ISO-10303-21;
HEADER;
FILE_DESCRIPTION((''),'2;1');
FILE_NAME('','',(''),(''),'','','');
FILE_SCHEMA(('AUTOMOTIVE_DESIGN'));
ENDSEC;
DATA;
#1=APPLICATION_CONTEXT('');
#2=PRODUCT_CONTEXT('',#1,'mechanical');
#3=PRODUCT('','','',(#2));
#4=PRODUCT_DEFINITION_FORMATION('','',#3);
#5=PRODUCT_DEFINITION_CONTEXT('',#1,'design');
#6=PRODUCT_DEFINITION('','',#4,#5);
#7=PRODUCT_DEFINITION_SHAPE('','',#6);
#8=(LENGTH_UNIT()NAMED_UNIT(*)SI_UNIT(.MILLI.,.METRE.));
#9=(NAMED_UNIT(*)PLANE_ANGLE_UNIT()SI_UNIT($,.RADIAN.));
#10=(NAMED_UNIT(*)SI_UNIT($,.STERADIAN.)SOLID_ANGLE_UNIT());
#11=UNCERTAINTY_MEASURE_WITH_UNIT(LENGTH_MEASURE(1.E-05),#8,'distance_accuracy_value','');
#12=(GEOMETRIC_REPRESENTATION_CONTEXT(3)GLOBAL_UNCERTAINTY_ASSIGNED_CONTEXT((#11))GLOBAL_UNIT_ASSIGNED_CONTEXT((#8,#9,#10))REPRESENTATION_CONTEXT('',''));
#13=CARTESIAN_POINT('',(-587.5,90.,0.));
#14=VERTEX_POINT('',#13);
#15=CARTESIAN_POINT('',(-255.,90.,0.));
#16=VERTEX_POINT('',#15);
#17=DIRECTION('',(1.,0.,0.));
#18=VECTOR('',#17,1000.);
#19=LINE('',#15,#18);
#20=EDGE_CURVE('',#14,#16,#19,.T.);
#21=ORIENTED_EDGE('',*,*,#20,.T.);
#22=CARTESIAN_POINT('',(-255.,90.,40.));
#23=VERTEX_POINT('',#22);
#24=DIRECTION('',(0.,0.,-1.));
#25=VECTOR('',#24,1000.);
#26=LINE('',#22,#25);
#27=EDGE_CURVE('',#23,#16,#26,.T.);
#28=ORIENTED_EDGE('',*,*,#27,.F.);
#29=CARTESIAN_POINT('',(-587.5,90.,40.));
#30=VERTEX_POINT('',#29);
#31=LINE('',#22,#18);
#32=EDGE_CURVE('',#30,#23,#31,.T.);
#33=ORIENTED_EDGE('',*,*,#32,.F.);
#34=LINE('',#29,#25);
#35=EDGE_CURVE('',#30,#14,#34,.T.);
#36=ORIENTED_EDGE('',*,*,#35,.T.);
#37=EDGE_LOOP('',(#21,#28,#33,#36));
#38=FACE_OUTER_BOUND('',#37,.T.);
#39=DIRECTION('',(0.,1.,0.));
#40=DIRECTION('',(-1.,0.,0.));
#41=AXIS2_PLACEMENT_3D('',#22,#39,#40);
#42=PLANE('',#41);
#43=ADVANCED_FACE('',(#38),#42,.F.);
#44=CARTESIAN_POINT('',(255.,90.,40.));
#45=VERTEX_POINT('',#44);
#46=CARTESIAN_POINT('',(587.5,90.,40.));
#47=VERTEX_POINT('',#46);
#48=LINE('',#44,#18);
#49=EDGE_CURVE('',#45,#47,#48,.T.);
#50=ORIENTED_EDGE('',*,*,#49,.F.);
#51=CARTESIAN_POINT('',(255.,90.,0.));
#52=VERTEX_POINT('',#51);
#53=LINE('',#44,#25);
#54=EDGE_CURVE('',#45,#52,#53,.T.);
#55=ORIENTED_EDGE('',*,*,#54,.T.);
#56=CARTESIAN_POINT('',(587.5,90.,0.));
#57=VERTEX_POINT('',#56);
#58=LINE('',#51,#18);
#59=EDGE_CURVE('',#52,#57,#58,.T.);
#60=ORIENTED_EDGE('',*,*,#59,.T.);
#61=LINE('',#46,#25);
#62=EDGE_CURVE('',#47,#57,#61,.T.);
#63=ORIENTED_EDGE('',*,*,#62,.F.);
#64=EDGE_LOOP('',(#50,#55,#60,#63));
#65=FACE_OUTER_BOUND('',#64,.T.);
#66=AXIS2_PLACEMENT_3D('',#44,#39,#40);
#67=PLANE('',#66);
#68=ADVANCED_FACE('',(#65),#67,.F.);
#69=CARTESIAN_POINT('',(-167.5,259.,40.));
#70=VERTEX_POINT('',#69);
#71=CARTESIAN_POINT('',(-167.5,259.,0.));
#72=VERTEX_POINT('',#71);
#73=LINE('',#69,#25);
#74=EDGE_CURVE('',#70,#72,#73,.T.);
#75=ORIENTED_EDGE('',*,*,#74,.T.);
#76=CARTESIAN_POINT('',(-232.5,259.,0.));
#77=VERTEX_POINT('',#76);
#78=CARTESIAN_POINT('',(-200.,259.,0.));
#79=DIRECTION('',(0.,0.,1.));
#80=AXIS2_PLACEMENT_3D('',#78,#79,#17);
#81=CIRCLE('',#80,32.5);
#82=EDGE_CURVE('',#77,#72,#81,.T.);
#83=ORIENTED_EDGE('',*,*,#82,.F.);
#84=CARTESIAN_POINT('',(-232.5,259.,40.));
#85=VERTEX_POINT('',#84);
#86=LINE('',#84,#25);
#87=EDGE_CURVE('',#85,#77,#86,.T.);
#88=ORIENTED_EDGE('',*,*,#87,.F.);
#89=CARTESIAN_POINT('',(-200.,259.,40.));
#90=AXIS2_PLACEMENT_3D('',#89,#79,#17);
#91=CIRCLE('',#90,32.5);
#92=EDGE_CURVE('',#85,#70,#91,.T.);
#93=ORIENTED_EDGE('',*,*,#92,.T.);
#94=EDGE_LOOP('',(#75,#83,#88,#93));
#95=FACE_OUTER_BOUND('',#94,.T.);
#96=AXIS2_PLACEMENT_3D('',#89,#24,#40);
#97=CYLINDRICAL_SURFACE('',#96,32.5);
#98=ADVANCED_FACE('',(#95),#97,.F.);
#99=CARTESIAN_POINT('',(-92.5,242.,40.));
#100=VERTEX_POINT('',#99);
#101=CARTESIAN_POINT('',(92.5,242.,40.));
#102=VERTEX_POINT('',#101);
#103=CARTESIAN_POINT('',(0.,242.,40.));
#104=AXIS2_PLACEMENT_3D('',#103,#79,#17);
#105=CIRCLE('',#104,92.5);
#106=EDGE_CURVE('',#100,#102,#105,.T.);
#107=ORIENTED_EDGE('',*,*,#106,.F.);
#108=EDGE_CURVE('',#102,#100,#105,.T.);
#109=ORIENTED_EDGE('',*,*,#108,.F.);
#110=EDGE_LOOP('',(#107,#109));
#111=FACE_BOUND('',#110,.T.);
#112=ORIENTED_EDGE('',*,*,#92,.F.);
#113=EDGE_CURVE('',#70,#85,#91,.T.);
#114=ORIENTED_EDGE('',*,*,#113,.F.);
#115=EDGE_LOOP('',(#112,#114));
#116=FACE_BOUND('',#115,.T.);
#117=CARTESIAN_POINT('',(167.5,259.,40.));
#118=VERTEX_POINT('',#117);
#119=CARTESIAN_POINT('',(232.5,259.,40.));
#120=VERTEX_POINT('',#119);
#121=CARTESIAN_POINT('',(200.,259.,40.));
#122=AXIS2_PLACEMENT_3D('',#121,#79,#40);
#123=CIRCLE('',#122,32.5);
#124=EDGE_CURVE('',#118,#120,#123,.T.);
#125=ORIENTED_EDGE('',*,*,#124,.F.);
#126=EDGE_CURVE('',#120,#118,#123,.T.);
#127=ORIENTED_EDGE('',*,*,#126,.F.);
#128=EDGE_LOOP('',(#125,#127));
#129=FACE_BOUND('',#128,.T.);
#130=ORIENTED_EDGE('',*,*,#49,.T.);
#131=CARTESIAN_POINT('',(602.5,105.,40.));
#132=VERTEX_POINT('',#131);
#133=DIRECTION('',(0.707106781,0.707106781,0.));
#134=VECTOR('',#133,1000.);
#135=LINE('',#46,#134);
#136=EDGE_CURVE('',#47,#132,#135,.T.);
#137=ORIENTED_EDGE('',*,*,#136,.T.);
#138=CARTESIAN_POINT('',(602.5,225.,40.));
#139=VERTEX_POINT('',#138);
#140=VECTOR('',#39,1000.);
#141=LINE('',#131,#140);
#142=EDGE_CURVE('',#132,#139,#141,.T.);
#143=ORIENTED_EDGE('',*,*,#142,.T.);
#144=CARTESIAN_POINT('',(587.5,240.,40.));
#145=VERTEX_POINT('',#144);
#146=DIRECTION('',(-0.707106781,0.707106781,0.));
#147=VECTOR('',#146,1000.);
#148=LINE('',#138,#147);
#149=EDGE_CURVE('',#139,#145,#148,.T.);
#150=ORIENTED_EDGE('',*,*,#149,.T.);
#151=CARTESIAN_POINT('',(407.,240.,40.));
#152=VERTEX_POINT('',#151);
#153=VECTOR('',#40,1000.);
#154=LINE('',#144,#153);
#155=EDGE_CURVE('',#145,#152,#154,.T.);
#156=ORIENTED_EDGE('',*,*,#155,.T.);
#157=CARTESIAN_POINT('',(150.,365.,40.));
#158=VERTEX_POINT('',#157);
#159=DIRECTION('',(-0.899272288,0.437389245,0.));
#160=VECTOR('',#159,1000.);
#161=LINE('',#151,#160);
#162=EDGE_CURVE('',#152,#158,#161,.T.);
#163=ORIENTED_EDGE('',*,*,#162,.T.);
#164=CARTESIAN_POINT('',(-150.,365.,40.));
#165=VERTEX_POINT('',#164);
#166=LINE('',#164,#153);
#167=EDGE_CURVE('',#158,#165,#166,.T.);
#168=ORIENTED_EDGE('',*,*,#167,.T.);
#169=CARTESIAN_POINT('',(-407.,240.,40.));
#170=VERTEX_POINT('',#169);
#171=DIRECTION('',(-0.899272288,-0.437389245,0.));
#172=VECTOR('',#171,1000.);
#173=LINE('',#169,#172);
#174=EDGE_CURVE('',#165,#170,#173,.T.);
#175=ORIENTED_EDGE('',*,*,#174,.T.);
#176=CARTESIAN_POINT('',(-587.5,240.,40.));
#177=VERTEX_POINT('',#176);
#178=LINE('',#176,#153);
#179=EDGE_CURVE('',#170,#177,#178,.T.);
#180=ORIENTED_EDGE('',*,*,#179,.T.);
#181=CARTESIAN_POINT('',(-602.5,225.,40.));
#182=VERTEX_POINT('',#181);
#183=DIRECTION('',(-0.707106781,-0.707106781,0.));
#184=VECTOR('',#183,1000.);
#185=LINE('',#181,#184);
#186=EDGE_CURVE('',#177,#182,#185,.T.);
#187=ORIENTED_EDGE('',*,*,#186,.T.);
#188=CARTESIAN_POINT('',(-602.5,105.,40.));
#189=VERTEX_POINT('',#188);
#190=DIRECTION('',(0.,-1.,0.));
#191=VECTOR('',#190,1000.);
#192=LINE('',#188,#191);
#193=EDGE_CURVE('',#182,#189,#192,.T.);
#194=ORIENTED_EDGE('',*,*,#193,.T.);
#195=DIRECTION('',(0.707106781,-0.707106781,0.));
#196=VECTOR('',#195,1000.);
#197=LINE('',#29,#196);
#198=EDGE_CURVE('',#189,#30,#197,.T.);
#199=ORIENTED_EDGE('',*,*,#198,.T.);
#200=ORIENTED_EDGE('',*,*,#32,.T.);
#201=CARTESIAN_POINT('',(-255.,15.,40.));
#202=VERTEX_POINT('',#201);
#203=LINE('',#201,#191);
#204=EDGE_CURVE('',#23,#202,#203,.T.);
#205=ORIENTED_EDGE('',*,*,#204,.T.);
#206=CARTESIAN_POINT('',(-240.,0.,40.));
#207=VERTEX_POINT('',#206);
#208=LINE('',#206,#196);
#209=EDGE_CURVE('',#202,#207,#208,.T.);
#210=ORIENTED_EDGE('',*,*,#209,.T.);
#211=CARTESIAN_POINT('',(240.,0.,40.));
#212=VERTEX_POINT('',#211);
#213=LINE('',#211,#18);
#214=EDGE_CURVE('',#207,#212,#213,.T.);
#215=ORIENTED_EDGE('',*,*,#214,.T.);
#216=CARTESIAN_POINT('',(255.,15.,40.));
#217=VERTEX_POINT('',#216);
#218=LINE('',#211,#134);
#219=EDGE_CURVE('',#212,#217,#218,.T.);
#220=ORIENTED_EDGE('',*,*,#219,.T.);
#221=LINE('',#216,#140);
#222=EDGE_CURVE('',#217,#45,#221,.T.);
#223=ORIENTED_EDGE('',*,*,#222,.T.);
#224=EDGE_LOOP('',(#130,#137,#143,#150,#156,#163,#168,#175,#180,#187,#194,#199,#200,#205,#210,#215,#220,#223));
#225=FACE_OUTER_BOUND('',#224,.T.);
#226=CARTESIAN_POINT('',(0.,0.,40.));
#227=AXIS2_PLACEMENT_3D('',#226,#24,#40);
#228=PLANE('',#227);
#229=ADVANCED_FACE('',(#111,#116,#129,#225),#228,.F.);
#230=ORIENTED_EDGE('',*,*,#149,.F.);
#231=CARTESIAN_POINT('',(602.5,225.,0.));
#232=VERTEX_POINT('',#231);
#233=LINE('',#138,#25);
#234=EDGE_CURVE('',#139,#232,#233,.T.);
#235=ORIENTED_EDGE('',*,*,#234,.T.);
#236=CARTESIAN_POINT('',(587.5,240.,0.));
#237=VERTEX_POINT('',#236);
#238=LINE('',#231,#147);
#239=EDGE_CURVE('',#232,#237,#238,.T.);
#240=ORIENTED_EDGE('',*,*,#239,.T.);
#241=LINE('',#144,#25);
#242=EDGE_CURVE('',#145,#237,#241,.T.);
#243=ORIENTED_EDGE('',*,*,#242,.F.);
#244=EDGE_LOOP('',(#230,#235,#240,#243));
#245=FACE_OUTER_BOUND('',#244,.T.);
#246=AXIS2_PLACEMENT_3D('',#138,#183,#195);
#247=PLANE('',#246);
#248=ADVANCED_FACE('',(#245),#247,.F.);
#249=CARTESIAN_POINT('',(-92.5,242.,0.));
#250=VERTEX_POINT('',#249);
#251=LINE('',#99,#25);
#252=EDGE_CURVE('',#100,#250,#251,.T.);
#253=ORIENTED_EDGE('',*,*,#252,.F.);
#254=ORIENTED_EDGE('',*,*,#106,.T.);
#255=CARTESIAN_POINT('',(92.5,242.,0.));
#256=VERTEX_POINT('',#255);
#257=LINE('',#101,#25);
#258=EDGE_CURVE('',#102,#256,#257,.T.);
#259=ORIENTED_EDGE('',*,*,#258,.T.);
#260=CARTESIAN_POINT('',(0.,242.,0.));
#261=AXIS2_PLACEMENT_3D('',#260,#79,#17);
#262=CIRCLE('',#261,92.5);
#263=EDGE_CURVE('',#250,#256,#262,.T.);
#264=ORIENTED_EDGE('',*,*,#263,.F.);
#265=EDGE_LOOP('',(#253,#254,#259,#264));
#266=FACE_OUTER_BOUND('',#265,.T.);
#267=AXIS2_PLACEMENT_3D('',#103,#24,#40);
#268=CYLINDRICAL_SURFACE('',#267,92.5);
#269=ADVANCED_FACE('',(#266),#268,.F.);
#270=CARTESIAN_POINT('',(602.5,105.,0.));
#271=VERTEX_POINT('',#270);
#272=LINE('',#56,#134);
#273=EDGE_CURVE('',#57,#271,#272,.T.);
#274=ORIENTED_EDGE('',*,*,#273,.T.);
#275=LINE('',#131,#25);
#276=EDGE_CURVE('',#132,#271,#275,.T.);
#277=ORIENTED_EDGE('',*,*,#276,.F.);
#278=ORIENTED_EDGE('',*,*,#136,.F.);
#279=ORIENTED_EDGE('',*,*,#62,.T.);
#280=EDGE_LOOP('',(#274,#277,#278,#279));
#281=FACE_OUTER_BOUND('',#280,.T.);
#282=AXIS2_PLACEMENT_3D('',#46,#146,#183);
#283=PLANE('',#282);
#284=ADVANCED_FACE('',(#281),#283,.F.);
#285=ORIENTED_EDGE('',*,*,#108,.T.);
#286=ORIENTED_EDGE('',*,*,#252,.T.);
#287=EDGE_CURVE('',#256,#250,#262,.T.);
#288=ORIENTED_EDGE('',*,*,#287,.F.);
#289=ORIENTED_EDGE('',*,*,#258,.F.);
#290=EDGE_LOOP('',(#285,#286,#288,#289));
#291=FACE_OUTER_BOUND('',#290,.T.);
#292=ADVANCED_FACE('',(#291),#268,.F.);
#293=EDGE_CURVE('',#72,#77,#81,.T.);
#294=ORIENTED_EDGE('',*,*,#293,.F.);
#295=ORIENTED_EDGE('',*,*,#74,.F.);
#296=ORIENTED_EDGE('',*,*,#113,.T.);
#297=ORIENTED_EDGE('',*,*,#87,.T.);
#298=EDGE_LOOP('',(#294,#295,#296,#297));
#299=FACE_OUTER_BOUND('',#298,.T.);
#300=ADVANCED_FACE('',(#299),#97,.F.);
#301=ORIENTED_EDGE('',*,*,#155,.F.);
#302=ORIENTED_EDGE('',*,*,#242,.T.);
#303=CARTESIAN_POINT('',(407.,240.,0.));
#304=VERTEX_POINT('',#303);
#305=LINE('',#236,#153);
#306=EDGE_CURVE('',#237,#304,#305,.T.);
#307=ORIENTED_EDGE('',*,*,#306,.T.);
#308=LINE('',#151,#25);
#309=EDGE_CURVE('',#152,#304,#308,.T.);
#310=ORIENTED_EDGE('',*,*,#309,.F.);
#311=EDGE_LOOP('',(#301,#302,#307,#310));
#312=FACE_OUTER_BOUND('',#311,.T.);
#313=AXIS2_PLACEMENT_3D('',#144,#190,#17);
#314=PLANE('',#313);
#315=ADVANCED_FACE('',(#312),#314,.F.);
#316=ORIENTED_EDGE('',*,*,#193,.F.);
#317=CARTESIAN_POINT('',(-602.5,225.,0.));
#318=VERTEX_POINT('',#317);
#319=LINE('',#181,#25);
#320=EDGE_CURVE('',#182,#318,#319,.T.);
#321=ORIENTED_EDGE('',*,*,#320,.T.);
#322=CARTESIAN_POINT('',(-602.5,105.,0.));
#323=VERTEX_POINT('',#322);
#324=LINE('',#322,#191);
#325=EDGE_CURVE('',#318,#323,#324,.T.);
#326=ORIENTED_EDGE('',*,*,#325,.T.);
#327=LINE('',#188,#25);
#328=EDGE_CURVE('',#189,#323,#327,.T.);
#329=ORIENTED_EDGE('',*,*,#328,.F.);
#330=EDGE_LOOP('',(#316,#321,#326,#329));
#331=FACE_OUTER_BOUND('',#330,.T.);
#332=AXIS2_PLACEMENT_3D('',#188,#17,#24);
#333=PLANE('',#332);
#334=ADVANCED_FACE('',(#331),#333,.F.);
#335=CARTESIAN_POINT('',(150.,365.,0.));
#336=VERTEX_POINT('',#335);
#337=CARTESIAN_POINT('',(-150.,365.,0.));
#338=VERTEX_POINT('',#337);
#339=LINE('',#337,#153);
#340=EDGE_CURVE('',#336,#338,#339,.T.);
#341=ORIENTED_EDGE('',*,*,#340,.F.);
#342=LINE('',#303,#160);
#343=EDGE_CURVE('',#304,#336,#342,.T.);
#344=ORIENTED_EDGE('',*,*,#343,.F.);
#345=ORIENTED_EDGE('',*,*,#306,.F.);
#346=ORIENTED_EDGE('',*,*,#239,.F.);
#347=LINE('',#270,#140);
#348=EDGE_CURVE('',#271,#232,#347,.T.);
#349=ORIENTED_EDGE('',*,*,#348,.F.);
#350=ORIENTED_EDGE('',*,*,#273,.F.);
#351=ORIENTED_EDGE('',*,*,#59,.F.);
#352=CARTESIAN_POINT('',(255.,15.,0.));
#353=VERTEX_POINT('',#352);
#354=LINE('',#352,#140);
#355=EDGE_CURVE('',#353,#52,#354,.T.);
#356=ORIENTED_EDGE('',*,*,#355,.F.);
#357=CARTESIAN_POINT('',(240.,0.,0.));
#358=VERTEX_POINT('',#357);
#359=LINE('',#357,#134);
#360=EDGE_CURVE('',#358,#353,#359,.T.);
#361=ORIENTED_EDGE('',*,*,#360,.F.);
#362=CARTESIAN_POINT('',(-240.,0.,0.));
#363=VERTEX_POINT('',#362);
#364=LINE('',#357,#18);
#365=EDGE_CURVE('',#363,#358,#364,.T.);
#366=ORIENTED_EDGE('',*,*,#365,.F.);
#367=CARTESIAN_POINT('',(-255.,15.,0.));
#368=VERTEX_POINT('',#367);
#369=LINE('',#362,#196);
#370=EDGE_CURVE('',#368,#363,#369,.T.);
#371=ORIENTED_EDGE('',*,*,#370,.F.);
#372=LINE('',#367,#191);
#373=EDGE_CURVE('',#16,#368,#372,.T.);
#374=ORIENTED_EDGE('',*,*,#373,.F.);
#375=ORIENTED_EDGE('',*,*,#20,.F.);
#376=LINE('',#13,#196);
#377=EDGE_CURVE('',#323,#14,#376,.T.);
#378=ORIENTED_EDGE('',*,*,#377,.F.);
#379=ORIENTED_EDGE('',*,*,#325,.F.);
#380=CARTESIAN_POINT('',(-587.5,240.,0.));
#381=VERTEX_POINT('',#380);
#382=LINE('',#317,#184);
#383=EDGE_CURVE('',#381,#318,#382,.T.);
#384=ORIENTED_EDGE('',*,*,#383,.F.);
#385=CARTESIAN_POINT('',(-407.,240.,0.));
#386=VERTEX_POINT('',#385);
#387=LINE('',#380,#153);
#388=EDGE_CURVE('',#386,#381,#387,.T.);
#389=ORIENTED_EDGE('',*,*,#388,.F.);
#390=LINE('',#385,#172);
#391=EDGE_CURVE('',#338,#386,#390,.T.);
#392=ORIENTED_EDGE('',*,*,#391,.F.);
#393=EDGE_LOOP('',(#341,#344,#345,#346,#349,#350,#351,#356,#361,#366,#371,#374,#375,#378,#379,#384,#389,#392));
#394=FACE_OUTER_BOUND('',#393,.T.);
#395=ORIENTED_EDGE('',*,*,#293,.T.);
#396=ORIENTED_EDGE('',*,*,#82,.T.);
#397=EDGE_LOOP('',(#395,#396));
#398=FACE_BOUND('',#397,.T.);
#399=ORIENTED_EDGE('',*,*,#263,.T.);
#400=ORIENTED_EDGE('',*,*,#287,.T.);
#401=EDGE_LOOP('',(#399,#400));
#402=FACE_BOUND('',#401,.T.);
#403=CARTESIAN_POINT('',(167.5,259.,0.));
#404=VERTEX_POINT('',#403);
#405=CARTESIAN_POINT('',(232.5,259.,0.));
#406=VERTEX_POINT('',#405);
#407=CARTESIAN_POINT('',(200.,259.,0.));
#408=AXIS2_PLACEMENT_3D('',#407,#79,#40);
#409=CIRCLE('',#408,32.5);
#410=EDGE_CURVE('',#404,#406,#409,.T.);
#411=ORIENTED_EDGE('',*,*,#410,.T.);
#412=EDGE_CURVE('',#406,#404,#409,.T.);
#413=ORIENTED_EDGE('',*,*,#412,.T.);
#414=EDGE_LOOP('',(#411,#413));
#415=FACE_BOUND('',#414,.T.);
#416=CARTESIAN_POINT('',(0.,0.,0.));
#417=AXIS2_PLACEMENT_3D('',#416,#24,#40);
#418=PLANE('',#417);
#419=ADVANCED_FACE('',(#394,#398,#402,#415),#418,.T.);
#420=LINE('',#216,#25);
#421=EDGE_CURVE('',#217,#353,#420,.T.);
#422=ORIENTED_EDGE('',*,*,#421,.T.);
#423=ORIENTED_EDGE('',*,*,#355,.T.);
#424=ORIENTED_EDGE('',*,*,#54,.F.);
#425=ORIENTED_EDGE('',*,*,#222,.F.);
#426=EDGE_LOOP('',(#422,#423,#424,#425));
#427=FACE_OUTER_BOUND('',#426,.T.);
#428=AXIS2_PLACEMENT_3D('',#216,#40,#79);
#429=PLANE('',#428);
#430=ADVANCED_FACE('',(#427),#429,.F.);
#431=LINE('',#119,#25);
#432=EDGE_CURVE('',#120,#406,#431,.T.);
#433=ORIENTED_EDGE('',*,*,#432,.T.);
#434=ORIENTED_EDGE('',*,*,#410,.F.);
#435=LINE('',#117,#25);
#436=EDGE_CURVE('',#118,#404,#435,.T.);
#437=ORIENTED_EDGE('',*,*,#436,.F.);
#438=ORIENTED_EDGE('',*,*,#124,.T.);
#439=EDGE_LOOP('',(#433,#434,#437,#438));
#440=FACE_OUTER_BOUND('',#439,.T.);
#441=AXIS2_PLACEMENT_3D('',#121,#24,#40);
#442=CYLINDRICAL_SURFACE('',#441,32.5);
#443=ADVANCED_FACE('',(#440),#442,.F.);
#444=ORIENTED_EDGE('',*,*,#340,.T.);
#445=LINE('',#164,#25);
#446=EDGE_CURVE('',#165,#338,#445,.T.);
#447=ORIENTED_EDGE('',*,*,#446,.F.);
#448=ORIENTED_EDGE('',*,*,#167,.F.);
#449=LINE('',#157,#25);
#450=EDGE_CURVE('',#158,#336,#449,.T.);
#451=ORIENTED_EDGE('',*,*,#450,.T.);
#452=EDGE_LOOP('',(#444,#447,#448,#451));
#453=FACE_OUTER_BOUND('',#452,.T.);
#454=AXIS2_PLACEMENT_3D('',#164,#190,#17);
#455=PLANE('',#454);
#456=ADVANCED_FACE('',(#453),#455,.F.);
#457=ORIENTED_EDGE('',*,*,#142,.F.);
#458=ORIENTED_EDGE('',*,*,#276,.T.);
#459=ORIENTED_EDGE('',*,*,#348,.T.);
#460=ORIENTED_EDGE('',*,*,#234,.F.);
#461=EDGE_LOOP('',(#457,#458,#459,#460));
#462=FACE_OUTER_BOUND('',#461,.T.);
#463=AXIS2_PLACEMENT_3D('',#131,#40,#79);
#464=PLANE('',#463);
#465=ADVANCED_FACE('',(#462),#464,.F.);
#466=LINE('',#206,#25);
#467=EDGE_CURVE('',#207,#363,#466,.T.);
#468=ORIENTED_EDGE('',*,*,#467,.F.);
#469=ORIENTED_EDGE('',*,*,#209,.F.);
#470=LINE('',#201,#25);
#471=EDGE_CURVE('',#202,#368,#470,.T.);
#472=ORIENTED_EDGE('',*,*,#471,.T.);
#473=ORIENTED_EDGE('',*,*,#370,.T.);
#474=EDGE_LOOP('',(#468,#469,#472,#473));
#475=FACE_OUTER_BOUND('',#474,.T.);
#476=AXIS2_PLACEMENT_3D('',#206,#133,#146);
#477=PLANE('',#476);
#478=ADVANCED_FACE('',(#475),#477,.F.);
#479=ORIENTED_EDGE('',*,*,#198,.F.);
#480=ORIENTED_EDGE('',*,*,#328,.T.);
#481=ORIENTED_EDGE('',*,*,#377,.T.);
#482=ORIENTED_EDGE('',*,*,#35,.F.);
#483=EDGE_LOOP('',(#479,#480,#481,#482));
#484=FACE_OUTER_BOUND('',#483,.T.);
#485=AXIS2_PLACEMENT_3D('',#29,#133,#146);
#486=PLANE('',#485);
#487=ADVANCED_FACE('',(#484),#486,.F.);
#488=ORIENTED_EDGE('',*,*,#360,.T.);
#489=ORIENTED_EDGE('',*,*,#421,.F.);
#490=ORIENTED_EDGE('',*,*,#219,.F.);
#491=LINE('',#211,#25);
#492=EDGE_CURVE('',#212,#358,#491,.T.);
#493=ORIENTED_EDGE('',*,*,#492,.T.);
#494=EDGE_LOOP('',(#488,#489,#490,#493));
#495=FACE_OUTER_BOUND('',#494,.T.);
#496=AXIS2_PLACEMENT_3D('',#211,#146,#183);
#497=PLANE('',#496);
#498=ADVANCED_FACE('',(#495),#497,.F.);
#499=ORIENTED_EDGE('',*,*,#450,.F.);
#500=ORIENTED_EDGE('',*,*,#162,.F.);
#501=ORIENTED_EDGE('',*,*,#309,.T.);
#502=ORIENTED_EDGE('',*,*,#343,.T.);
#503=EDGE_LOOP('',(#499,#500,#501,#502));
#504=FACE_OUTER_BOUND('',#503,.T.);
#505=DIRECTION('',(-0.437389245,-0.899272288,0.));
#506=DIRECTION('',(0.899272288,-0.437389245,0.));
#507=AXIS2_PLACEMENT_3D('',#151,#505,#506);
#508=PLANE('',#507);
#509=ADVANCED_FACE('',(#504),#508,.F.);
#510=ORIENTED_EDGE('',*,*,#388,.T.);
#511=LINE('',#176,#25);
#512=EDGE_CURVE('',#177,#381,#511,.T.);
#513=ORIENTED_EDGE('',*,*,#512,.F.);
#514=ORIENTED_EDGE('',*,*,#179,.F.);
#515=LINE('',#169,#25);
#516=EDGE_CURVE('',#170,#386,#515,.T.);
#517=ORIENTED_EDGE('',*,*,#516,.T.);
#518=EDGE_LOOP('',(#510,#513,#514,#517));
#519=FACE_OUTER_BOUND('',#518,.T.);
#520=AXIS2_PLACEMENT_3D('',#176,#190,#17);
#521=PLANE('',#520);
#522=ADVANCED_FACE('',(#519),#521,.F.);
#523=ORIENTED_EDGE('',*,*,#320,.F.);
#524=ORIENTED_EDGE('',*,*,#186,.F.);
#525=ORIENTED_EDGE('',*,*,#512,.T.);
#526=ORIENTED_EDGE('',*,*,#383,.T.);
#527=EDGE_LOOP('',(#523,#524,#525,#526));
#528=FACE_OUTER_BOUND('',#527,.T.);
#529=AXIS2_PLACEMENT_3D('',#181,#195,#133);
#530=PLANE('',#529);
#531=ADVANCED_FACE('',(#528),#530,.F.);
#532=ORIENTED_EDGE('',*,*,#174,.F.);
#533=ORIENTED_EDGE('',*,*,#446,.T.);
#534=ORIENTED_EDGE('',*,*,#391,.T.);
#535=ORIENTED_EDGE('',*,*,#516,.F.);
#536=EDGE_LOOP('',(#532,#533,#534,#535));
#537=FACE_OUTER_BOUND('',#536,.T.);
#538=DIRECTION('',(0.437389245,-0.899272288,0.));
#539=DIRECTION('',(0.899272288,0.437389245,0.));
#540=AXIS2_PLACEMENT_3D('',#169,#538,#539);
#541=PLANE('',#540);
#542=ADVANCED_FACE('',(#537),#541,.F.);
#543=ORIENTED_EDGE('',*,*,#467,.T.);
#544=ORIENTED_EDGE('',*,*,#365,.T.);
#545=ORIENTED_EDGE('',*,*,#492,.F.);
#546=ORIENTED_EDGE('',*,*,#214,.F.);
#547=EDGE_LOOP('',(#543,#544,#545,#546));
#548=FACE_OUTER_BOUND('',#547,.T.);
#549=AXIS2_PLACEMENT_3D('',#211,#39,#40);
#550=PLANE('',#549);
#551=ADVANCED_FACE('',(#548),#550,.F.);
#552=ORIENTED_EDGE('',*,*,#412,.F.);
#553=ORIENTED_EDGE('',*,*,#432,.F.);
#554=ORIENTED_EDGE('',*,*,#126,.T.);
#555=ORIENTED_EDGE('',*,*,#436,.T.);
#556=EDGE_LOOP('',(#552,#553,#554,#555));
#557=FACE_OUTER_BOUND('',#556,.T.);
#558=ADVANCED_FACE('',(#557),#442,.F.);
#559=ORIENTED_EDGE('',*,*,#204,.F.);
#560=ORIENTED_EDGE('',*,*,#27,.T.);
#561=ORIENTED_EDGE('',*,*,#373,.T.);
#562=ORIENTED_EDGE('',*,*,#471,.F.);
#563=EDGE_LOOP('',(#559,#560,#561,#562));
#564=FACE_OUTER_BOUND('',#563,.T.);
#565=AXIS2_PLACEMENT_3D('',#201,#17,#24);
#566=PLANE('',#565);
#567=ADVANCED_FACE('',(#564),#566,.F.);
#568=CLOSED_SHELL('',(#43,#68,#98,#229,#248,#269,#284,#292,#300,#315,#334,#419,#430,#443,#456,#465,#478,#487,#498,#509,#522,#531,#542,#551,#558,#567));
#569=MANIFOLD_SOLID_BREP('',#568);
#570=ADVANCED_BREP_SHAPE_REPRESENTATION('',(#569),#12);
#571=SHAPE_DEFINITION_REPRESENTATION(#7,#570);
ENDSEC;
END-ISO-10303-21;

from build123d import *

# Parameters (mm, degrees)
SKETCH1_R           = 32.5
SKETCH1_R_2         = 92.5
BOSS_EXTRUDE1_DEPTH = 40


with BuildPart() as part:
    # Sketch1 → Boss-Extrude1 (new body)
    with BuildSketch(Plane.XY):
        Polygon((240, 0), (-240, 0), (-255, 15), (-255, 90), (-587.5, 90), (-602.5, 105), (-602.5, 225), (-587.5, 240), (-407, 240), (-150, 365), (150, 365), (407, 240), (587.5, 240), (602.5, 225), (602.5, 105), (587.5, 90), (255, 90), (255, 15), align=None)
        with Locations((-200, 259)):
            Circle(SKETCH1_R, mode=Mode.SUBTRACT)
        with Locations(Location((200, 259, 0), (0, 0, 180))):
            Circle(SKETCH1_R, mode=Mode.SUBTRACT)
        with Locations((0, 242)):
            Circle(SKETCH1_R_2, mode=Mode.SUBTRACT)
    extrude(amount=BOSS_EXTRUDE1_DEPTH)


solid = part.part
